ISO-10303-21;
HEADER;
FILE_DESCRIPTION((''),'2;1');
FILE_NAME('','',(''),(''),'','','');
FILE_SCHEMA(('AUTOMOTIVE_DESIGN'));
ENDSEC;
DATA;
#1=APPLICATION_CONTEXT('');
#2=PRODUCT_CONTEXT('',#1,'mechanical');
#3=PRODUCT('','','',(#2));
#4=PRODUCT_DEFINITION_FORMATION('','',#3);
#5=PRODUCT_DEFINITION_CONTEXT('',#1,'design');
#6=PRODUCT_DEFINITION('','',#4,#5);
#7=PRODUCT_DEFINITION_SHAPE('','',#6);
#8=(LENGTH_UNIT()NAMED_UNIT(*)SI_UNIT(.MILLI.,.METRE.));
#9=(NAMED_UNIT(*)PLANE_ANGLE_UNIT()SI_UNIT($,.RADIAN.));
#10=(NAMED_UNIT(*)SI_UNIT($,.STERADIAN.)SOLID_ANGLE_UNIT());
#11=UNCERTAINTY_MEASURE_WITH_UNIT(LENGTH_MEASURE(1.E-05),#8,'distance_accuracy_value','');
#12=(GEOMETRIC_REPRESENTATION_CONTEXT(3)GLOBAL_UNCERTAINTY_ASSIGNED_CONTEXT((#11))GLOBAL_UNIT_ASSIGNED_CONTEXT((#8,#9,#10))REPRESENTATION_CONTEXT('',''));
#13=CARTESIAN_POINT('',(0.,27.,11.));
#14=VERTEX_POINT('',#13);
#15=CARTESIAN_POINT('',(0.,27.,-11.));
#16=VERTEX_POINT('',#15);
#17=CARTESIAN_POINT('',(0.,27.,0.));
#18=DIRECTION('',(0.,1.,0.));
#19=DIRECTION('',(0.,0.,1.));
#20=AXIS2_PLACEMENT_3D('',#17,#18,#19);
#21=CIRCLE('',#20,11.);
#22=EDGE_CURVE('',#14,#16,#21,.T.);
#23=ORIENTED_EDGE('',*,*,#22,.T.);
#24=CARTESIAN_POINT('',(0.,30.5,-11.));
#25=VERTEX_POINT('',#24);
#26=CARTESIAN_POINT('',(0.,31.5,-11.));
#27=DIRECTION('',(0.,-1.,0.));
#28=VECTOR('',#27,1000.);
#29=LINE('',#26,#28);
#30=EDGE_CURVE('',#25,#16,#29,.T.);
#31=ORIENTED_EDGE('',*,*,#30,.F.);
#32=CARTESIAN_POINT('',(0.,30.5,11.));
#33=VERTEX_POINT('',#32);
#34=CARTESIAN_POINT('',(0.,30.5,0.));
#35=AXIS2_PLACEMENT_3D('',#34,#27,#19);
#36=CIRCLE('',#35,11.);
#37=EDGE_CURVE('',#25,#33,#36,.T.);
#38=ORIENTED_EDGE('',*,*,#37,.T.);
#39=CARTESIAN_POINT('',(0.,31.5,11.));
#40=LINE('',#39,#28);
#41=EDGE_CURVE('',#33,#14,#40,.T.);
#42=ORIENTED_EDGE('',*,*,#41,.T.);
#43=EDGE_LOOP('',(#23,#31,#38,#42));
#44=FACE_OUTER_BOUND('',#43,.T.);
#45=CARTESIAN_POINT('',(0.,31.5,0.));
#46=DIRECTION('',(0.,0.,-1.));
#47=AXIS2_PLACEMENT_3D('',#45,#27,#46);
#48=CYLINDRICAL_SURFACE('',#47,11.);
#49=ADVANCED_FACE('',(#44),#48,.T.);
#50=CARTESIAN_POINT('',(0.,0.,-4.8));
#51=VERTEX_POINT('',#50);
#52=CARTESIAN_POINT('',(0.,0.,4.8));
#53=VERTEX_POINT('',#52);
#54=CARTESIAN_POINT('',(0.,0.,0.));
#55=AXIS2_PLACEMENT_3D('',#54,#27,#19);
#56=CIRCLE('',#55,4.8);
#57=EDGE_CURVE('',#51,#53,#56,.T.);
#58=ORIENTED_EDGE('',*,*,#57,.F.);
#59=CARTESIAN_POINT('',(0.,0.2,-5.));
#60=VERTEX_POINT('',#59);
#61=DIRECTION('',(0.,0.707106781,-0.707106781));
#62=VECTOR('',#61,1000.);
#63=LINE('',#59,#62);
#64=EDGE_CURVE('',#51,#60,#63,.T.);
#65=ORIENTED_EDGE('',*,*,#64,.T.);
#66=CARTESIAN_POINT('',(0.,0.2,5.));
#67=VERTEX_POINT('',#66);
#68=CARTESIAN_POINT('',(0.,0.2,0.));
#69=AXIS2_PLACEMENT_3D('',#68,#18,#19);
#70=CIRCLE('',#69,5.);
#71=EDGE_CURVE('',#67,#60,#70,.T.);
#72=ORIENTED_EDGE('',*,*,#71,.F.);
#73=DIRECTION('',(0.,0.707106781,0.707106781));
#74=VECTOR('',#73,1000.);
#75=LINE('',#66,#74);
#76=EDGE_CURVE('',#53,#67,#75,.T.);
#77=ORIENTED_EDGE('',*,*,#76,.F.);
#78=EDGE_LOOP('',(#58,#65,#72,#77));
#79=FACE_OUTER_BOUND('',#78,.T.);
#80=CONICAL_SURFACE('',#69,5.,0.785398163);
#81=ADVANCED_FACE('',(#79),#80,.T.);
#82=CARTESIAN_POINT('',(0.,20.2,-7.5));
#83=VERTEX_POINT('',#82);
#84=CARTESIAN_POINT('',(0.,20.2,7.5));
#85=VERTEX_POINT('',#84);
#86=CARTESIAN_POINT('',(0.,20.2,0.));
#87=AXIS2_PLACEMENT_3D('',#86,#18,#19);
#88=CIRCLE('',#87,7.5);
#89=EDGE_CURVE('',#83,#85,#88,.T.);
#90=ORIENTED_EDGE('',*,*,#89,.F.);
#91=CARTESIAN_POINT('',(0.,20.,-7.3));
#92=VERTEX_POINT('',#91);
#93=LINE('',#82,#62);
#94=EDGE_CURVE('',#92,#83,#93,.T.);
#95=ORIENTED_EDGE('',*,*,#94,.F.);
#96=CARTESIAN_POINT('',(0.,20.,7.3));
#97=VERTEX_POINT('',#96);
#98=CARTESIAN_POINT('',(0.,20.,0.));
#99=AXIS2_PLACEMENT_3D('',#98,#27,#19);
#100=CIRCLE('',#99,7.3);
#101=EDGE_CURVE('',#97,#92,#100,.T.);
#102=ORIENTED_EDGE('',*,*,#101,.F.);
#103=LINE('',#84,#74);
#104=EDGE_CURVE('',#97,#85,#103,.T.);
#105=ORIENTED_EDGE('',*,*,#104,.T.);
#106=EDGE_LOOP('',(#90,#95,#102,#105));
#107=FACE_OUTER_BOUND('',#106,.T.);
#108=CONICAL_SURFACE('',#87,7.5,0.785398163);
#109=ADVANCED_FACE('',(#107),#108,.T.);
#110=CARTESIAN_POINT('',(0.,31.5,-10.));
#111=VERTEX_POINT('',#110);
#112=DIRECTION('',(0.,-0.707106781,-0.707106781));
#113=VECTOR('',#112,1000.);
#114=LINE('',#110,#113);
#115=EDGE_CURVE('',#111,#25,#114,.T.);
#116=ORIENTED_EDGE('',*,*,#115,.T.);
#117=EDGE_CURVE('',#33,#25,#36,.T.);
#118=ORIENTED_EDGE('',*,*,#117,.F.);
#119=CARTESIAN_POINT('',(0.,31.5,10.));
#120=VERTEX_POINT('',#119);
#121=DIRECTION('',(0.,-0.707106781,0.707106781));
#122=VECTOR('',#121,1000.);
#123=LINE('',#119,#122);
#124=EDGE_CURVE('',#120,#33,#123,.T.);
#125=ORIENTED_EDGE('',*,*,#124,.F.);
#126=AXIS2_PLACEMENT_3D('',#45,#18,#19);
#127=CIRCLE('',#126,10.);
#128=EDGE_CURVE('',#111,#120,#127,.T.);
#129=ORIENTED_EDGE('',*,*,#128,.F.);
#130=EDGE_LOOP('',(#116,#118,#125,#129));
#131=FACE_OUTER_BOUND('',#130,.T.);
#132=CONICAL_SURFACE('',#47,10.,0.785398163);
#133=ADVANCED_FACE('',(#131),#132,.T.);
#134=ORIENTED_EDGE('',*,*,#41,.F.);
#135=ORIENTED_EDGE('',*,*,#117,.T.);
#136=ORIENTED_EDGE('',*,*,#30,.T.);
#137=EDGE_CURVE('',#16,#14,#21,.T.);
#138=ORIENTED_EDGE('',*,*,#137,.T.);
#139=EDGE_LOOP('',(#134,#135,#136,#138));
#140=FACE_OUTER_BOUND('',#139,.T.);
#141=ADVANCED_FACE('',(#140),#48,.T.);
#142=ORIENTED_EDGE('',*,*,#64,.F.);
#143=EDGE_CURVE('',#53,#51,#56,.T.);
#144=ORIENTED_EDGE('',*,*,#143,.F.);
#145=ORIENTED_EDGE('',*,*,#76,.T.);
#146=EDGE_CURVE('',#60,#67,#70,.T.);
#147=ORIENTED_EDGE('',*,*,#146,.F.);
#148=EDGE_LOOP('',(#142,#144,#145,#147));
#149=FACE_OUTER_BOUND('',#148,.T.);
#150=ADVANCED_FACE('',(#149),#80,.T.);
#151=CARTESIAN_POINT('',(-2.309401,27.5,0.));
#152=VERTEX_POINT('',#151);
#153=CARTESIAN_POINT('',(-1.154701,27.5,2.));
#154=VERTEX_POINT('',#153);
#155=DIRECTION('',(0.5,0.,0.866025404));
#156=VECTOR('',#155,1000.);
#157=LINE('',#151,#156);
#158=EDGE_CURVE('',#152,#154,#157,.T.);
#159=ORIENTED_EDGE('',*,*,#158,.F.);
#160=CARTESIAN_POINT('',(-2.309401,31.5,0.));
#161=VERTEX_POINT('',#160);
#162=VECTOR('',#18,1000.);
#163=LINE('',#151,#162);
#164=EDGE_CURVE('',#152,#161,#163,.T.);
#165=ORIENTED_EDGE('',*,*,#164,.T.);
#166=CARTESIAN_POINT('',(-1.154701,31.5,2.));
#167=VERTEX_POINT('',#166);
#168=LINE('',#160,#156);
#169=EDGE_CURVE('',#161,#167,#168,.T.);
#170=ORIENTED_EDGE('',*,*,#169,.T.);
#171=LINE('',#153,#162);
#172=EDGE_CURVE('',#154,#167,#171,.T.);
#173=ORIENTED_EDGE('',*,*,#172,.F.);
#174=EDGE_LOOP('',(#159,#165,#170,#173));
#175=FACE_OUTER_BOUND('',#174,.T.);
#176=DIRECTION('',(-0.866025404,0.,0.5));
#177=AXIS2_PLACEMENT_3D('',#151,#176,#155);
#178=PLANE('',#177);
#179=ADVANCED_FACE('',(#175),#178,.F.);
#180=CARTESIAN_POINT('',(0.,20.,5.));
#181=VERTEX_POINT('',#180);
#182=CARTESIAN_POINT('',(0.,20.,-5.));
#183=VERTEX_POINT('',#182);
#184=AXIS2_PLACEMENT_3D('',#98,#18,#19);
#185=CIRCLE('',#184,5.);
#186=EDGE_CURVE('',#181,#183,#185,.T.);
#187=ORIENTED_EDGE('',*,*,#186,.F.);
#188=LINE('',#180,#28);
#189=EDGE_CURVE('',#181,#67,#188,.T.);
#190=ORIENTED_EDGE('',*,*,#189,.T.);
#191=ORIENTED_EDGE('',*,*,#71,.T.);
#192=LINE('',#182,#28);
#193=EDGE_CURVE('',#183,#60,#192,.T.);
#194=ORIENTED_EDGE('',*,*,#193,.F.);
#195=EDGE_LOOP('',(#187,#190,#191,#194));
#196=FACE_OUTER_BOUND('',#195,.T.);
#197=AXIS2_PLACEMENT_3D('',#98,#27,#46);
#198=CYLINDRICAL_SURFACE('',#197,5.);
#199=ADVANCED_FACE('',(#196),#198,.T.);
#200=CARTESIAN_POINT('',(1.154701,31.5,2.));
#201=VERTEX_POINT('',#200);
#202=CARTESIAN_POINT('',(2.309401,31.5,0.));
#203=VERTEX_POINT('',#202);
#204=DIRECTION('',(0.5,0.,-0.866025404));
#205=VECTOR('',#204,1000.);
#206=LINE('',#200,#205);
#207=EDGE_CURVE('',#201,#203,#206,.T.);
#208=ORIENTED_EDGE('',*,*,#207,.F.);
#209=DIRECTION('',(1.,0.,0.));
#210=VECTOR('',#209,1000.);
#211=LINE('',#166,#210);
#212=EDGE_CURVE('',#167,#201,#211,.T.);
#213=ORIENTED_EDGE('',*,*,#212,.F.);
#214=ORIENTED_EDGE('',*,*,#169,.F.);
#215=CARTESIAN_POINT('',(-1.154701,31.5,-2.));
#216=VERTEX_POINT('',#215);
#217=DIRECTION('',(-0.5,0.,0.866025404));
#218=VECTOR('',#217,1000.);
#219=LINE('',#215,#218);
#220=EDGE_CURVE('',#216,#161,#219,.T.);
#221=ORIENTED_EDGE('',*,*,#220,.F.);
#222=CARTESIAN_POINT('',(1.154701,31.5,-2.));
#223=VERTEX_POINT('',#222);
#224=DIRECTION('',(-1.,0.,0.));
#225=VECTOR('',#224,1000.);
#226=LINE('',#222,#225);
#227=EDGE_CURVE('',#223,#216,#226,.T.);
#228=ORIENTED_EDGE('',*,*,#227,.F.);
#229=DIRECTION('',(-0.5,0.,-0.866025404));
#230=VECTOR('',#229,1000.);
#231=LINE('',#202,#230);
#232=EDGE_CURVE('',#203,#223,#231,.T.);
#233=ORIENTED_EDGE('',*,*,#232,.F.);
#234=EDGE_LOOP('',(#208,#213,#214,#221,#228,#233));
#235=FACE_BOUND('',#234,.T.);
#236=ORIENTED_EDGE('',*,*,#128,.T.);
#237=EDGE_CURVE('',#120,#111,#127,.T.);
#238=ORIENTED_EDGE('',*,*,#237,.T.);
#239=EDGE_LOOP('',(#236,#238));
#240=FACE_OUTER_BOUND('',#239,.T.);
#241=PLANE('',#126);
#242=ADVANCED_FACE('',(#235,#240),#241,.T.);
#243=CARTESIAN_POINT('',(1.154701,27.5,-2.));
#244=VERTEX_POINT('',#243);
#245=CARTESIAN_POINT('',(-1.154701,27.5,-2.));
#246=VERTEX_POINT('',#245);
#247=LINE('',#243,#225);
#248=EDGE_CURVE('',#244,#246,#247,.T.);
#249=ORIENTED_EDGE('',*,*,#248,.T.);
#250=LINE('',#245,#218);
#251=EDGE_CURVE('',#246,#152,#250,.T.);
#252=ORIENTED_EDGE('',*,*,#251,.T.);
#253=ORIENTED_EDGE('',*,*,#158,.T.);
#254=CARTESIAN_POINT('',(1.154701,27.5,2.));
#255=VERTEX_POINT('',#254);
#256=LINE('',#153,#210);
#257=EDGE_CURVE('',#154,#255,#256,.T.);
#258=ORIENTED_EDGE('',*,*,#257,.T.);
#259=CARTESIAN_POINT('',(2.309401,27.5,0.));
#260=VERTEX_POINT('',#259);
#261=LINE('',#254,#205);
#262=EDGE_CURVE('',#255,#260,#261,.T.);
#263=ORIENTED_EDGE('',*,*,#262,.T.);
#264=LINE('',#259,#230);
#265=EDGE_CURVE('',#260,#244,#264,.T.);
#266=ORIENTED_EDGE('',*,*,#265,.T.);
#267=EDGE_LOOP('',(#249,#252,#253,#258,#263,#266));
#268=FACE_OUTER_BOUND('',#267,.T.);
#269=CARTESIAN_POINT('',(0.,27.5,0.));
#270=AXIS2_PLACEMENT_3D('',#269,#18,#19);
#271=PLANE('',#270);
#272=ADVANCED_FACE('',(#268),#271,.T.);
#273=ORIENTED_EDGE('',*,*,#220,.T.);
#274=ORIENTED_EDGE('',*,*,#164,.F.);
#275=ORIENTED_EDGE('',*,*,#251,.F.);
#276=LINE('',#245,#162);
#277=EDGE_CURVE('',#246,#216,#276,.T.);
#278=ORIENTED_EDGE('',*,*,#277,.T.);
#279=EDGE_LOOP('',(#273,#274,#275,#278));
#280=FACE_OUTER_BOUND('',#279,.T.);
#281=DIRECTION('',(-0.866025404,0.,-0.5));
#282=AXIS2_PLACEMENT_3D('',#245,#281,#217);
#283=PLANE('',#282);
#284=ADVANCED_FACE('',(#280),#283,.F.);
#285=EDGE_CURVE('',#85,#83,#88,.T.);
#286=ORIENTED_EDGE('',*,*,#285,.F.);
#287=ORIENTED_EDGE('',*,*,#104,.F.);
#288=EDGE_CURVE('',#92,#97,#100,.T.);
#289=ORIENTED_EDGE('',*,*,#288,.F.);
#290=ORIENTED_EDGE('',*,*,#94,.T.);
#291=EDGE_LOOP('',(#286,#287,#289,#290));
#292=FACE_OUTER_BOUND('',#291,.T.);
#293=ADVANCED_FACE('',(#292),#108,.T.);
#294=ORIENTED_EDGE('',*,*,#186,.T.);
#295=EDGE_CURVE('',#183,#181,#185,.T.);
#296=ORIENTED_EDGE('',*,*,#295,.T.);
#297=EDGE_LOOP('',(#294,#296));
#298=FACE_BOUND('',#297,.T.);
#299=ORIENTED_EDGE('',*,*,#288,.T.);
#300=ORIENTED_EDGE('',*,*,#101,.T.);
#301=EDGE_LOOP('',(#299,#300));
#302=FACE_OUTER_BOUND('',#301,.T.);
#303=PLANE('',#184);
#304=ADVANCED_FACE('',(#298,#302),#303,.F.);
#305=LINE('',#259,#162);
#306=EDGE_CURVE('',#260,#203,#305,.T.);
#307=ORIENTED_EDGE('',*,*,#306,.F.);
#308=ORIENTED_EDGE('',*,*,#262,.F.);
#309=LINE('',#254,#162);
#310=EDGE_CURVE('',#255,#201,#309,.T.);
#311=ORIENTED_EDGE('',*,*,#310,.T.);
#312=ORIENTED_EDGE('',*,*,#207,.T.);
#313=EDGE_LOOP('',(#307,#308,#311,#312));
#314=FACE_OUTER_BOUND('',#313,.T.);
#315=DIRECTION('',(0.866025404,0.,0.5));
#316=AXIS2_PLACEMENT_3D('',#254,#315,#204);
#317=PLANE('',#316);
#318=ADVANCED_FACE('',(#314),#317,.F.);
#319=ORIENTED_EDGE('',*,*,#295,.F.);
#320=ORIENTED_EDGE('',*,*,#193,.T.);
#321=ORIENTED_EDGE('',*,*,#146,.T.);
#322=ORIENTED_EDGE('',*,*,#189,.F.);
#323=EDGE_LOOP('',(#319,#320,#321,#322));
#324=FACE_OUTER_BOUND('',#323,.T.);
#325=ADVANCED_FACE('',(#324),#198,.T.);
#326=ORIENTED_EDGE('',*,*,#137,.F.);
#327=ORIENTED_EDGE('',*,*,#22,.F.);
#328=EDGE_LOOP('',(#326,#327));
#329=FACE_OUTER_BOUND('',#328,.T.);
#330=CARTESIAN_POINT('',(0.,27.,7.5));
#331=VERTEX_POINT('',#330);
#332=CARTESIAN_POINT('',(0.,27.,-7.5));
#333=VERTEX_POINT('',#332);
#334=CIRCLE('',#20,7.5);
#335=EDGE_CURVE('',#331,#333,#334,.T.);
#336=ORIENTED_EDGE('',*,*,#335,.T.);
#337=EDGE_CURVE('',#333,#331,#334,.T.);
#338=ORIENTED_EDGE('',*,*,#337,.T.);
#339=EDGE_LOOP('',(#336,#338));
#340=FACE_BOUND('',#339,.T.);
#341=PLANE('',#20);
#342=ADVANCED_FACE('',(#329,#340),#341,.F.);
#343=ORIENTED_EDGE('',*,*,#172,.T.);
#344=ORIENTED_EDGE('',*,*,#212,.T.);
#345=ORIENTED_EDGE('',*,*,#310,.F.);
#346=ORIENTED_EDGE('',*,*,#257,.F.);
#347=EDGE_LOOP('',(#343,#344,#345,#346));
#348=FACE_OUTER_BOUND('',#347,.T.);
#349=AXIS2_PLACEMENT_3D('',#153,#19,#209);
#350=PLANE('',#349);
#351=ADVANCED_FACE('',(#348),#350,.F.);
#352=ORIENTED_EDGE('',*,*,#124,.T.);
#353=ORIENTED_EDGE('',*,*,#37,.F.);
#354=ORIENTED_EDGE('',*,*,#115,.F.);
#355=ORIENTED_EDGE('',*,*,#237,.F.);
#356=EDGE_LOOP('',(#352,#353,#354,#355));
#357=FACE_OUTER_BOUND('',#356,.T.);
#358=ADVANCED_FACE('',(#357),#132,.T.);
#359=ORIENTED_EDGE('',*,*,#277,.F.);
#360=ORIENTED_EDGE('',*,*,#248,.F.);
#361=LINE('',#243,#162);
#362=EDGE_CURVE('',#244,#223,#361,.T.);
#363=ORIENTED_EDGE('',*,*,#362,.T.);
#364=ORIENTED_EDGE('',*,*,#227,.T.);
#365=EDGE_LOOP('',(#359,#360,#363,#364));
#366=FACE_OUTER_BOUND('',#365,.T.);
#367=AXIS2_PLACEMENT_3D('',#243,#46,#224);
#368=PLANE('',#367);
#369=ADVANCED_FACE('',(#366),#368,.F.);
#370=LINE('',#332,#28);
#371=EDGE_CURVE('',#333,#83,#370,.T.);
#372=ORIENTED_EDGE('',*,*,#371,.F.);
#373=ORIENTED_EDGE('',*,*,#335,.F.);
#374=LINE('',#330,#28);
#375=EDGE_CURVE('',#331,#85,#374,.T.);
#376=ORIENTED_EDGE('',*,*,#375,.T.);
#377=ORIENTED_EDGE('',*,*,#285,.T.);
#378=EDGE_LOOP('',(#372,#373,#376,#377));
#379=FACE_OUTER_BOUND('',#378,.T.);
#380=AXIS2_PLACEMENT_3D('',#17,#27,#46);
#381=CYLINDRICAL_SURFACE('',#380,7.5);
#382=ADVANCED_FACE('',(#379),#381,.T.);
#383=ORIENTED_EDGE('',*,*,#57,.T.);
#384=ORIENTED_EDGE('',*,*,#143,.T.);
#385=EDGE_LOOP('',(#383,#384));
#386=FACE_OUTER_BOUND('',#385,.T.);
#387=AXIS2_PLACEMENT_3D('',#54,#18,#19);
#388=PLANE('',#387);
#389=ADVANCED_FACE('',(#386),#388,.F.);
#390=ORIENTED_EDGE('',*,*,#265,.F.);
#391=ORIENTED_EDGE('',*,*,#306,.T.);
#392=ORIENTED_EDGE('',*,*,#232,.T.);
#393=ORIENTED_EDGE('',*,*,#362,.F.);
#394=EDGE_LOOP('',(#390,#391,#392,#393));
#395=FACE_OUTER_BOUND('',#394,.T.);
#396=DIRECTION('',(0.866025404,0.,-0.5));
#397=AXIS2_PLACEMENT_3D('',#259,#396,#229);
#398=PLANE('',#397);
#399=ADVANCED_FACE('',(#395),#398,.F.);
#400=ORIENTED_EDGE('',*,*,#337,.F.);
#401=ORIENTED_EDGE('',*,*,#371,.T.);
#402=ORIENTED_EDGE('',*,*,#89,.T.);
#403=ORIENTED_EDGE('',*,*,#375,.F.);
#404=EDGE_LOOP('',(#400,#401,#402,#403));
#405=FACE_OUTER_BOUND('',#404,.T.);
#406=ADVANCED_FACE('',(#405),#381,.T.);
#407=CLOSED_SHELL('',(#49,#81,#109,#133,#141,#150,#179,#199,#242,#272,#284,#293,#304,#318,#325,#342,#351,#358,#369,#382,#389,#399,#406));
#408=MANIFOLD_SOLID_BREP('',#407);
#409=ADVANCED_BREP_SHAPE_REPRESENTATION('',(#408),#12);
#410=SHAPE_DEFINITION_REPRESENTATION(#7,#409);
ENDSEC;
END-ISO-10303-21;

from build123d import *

# Parameters (mm, degrees)
SKETCH_1_R          = 5
EXTRUDE_1_DEPTH     = 20
SKETCH_2_R          = 7.5
EXTRUDE_2_DEPTH     = 7
SKETCH_3_R          = 11
EXTRUDE_3_DEPTH     = 4.5
CHAMFER_1_SIZE      = 1
CHAMFER_2_SIZE      = 0.2
CHAMFER_3_SIZE      = 0.2
CUT_EXTRUDE_1_DEPTH = 4


with BuildPart() as part:
    # 草图1 → 凸台-拉伸1 (new body)
    with BuildSketch(Plane(origin=(0, 0, 0), x_dir=(1, 0, 0), z_dir=(0, 1, 0))):
        with Locations(Location((0, 0, 0), (0, 0, 270))):
            Circle(SKETCH_1_R)
    extrude(amount=EXTRUDE_1_DEPTH)

    # 草图2 → 凸台-拉伸2 (add)
    with BuildSketch(Plane(origin=(0, 20, 0), x_dir=(1, 0, 0), z_dir=(0, 1, 0))):
        with Locations(Location((0, 0, 0), (0, 0, 270))):
            Circle(SKETCH_2_R)
    extrude(amount=EXTRUDE_2_DEPTH)

    # 草图3 → 凸台-拉伸3 (add)
    with BuildSketch(Plane(origin=(0, 27, 0), x_dir=(1, 0, 0), z_dir=(0, 1, 0))):
        with Locations(Location((0, 0, 0), (0, 0, 270))):
            Circle(SKETCH_3_R)
    extrude(amount=EXTRUDE_3_DEPTH)

    # 倒角1
    chamfer_1_edges = [part.edges().sort_by_distance(p)[0] for p in [
        (0, 31.5, -11),
    ]]
    chamfer(chamfer_1_edges, length=CHAMFER_1_SIZE)

    # 倒角2
    chamfer_2_edges = [part.edges().sort_by_distance(p)[0] for p in [
        (0, 20, -7.5),
    ]]
    chamfer(chamfer_2_edges, length=CHAMFER_2_SIZE)

    # 倒角3
    chamfer_3_edges = [part.edges().sort_by_distance(p)[0] for p in [
        (0, 0, -5),
    ]]
    chamfer(chamfer_3_edges, length=CHAMFER_3_SIZE)

    # 草图4 → 切除-拉伸1 (cut)
    with BuildSketch(Plane(origin=(0, 31.5, 0), x_dir=(1, 0, 0), z_dir=(0, 1, 0))):
        Polygon((2.309401077, 0), (1.154700538, 2), (-1.154700538, 2), (-2.309401077, 0), (-1.154700538, -2), (1.154700538, -2), align=None)
    extrude(amount=-CUT_EXTRUDE_1_DEPTH, mode=Mode.SUBTRACT)


solid = part.part
